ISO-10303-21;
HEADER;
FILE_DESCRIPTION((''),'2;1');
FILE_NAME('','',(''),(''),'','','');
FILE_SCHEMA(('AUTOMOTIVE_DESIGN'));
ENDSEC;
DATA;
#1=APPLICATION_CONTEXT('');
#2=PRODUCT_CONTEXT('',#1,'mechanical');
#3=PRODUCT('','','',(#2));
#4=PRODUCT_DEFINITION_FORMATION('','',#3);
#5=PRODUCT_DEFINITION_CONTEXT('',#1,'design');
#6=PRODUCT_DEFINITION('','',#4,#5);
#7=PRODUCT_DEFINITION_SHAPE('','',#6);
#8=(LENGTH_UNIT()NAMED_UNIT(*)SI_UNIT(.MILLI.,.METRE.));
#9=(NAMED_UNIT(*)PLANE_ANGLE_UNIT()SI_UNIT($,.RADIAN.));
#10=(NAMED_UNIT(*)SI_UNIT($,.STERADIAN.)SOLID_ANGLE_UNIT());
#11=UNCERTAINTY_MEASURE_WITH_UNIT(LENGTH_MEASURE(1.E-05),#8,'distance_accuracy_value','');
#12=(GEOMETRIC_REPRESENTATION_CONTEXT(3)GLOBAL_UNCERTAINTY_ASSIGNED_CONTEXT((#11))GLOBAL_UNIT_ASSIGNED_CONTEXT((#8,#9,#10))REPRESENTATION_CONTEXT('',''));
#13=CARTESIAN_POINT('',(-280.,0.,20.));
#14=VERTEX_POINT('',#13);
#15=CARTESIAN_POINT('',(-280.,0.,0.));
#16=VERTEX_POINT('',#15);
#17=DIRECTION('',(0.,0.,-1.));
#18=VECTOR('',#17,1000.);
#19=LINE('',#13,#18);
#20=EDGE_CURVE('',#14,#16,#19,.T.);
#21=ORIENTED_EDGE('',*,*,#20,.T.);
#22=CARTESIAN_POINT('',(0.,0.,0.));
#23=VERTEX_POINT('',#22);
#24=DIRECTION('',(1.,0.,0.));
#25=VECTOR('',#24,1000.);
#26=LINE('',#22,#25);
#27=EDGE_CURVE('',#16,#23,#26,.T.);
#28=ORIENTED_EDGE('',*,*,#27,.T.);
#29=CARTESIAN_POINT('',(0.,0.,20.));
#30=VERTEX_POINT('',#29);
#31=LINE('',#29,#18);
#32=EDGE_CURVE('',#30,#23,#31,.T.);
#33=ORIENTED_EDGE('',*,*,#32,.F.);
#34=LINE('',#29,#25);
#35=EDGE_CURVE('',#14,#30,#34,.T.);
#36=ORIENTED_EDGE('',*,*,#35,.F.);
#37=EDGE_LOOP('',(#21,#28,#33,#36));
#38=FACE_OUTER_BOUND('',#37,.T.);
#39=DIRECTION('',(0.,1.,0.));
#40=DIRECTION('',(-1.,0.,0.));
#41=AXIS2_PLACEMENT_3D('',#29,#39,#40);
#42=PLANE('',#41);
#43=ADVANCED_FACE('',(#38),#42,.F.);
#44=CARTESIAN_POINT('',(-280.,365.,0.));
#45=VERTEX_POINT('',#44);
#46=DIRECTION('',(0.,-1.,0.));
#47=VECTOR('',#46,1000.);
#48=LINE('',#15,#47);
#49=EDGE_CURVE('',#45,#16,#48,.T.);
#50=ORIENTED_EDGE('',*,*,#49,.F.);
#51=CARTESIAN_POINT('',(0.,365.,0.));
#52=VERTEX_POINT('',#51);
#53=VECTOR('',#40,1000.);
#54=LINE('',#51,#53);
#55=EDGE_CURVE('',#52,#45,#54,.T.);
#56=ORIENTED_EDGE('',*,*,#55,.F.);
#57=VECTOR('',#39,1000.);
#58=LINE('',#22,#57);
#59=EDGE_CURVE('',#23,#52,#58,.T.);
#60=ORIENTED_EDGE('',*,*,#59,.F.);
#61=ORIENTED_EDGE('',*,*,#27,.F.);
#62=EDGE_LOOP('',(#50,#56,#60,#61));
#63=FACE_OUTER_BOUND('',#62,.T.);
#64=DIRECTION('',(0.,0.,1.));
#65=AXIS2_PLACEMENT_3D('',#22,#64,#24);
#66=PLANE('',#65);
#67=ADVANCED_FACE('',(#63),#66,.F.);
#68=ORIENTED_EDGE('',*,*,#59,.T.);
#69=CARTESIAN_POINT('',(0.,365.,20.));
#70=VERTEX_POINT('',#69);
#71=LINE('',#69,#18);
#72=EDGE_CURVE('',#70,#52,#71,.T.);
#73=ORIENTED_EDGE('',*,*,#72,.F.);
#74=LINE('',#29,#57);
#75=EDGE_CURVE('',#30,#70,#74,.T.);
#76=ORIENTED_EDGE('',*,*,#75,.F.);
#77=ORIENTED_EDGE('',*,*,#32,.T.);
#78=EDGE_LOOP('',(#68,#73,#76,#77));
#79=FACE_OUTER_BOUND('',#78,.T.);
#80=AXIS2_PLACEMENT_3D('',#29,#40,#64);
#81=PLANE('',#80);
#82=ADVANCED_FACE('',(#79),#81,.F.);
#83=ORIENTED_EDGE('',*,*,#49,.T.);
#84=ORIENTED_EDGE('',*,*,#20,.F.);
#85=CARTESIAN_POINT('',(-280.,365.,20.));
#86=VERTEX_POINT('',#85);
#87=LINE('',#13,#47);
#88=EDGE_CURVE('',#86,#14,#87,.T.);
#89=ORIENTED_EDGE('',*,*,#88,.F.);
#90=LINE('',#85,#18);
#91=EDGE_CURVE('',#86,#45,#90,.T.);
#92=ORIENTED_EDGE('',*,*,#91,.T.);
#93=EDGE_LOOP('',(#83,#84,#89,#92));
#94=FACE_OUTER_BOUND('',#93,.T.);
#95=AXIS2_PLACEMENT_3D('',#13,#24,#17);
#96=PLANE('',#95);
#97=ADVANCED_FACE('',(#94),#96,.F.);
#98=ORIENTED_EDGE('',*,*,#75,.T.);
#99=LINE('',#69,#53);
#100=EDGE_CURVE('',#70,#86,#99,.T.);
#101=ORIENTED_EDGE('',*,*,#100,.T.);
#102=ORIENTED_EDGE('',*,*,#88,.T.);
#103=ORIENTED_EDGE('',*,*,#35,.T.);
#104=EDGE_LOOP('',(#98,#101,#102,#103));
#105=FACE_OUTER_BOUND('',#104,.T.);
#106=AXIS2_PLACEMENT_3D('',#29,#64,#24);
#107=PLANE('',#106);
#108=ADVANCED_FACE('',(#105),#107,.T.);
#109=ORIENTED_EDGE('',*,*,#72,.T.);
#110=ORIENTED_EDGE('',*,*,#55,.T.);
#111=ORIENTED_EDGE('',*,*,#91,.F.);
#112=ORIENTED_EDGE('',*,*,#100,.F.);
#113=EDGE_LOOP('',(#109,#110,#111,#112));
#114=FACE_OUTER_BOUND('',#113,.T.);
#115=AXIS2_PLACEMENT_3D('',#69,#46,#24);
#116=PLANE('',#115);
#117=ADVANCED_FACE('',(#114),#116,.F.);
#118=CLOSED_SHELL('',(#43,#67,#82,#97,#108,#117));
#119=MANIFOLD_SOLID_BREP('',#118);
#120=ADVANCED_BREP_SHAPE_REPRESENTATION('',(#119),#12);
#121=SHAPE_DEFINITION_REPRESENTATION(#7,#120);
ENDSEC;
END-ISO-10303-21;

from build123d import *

# Parameters (mm, degrees)
SKETCH1_W           = 280
SKETCH1_H           = 365
BOSS_EXTRUDE1_DEPTH = 20


with BuildPart() as part:
    # Sketch1 → Boss-Extrude1 (new body)
    with BuildSketch(Plane.XY):
        with Locations((-140, 182.5)):
            Rectangle(SKETCH1_W, SKETCH1_H)
    extrude(amount=BOSS_EXTRUDE1_DEPTH)


solid = part.part
